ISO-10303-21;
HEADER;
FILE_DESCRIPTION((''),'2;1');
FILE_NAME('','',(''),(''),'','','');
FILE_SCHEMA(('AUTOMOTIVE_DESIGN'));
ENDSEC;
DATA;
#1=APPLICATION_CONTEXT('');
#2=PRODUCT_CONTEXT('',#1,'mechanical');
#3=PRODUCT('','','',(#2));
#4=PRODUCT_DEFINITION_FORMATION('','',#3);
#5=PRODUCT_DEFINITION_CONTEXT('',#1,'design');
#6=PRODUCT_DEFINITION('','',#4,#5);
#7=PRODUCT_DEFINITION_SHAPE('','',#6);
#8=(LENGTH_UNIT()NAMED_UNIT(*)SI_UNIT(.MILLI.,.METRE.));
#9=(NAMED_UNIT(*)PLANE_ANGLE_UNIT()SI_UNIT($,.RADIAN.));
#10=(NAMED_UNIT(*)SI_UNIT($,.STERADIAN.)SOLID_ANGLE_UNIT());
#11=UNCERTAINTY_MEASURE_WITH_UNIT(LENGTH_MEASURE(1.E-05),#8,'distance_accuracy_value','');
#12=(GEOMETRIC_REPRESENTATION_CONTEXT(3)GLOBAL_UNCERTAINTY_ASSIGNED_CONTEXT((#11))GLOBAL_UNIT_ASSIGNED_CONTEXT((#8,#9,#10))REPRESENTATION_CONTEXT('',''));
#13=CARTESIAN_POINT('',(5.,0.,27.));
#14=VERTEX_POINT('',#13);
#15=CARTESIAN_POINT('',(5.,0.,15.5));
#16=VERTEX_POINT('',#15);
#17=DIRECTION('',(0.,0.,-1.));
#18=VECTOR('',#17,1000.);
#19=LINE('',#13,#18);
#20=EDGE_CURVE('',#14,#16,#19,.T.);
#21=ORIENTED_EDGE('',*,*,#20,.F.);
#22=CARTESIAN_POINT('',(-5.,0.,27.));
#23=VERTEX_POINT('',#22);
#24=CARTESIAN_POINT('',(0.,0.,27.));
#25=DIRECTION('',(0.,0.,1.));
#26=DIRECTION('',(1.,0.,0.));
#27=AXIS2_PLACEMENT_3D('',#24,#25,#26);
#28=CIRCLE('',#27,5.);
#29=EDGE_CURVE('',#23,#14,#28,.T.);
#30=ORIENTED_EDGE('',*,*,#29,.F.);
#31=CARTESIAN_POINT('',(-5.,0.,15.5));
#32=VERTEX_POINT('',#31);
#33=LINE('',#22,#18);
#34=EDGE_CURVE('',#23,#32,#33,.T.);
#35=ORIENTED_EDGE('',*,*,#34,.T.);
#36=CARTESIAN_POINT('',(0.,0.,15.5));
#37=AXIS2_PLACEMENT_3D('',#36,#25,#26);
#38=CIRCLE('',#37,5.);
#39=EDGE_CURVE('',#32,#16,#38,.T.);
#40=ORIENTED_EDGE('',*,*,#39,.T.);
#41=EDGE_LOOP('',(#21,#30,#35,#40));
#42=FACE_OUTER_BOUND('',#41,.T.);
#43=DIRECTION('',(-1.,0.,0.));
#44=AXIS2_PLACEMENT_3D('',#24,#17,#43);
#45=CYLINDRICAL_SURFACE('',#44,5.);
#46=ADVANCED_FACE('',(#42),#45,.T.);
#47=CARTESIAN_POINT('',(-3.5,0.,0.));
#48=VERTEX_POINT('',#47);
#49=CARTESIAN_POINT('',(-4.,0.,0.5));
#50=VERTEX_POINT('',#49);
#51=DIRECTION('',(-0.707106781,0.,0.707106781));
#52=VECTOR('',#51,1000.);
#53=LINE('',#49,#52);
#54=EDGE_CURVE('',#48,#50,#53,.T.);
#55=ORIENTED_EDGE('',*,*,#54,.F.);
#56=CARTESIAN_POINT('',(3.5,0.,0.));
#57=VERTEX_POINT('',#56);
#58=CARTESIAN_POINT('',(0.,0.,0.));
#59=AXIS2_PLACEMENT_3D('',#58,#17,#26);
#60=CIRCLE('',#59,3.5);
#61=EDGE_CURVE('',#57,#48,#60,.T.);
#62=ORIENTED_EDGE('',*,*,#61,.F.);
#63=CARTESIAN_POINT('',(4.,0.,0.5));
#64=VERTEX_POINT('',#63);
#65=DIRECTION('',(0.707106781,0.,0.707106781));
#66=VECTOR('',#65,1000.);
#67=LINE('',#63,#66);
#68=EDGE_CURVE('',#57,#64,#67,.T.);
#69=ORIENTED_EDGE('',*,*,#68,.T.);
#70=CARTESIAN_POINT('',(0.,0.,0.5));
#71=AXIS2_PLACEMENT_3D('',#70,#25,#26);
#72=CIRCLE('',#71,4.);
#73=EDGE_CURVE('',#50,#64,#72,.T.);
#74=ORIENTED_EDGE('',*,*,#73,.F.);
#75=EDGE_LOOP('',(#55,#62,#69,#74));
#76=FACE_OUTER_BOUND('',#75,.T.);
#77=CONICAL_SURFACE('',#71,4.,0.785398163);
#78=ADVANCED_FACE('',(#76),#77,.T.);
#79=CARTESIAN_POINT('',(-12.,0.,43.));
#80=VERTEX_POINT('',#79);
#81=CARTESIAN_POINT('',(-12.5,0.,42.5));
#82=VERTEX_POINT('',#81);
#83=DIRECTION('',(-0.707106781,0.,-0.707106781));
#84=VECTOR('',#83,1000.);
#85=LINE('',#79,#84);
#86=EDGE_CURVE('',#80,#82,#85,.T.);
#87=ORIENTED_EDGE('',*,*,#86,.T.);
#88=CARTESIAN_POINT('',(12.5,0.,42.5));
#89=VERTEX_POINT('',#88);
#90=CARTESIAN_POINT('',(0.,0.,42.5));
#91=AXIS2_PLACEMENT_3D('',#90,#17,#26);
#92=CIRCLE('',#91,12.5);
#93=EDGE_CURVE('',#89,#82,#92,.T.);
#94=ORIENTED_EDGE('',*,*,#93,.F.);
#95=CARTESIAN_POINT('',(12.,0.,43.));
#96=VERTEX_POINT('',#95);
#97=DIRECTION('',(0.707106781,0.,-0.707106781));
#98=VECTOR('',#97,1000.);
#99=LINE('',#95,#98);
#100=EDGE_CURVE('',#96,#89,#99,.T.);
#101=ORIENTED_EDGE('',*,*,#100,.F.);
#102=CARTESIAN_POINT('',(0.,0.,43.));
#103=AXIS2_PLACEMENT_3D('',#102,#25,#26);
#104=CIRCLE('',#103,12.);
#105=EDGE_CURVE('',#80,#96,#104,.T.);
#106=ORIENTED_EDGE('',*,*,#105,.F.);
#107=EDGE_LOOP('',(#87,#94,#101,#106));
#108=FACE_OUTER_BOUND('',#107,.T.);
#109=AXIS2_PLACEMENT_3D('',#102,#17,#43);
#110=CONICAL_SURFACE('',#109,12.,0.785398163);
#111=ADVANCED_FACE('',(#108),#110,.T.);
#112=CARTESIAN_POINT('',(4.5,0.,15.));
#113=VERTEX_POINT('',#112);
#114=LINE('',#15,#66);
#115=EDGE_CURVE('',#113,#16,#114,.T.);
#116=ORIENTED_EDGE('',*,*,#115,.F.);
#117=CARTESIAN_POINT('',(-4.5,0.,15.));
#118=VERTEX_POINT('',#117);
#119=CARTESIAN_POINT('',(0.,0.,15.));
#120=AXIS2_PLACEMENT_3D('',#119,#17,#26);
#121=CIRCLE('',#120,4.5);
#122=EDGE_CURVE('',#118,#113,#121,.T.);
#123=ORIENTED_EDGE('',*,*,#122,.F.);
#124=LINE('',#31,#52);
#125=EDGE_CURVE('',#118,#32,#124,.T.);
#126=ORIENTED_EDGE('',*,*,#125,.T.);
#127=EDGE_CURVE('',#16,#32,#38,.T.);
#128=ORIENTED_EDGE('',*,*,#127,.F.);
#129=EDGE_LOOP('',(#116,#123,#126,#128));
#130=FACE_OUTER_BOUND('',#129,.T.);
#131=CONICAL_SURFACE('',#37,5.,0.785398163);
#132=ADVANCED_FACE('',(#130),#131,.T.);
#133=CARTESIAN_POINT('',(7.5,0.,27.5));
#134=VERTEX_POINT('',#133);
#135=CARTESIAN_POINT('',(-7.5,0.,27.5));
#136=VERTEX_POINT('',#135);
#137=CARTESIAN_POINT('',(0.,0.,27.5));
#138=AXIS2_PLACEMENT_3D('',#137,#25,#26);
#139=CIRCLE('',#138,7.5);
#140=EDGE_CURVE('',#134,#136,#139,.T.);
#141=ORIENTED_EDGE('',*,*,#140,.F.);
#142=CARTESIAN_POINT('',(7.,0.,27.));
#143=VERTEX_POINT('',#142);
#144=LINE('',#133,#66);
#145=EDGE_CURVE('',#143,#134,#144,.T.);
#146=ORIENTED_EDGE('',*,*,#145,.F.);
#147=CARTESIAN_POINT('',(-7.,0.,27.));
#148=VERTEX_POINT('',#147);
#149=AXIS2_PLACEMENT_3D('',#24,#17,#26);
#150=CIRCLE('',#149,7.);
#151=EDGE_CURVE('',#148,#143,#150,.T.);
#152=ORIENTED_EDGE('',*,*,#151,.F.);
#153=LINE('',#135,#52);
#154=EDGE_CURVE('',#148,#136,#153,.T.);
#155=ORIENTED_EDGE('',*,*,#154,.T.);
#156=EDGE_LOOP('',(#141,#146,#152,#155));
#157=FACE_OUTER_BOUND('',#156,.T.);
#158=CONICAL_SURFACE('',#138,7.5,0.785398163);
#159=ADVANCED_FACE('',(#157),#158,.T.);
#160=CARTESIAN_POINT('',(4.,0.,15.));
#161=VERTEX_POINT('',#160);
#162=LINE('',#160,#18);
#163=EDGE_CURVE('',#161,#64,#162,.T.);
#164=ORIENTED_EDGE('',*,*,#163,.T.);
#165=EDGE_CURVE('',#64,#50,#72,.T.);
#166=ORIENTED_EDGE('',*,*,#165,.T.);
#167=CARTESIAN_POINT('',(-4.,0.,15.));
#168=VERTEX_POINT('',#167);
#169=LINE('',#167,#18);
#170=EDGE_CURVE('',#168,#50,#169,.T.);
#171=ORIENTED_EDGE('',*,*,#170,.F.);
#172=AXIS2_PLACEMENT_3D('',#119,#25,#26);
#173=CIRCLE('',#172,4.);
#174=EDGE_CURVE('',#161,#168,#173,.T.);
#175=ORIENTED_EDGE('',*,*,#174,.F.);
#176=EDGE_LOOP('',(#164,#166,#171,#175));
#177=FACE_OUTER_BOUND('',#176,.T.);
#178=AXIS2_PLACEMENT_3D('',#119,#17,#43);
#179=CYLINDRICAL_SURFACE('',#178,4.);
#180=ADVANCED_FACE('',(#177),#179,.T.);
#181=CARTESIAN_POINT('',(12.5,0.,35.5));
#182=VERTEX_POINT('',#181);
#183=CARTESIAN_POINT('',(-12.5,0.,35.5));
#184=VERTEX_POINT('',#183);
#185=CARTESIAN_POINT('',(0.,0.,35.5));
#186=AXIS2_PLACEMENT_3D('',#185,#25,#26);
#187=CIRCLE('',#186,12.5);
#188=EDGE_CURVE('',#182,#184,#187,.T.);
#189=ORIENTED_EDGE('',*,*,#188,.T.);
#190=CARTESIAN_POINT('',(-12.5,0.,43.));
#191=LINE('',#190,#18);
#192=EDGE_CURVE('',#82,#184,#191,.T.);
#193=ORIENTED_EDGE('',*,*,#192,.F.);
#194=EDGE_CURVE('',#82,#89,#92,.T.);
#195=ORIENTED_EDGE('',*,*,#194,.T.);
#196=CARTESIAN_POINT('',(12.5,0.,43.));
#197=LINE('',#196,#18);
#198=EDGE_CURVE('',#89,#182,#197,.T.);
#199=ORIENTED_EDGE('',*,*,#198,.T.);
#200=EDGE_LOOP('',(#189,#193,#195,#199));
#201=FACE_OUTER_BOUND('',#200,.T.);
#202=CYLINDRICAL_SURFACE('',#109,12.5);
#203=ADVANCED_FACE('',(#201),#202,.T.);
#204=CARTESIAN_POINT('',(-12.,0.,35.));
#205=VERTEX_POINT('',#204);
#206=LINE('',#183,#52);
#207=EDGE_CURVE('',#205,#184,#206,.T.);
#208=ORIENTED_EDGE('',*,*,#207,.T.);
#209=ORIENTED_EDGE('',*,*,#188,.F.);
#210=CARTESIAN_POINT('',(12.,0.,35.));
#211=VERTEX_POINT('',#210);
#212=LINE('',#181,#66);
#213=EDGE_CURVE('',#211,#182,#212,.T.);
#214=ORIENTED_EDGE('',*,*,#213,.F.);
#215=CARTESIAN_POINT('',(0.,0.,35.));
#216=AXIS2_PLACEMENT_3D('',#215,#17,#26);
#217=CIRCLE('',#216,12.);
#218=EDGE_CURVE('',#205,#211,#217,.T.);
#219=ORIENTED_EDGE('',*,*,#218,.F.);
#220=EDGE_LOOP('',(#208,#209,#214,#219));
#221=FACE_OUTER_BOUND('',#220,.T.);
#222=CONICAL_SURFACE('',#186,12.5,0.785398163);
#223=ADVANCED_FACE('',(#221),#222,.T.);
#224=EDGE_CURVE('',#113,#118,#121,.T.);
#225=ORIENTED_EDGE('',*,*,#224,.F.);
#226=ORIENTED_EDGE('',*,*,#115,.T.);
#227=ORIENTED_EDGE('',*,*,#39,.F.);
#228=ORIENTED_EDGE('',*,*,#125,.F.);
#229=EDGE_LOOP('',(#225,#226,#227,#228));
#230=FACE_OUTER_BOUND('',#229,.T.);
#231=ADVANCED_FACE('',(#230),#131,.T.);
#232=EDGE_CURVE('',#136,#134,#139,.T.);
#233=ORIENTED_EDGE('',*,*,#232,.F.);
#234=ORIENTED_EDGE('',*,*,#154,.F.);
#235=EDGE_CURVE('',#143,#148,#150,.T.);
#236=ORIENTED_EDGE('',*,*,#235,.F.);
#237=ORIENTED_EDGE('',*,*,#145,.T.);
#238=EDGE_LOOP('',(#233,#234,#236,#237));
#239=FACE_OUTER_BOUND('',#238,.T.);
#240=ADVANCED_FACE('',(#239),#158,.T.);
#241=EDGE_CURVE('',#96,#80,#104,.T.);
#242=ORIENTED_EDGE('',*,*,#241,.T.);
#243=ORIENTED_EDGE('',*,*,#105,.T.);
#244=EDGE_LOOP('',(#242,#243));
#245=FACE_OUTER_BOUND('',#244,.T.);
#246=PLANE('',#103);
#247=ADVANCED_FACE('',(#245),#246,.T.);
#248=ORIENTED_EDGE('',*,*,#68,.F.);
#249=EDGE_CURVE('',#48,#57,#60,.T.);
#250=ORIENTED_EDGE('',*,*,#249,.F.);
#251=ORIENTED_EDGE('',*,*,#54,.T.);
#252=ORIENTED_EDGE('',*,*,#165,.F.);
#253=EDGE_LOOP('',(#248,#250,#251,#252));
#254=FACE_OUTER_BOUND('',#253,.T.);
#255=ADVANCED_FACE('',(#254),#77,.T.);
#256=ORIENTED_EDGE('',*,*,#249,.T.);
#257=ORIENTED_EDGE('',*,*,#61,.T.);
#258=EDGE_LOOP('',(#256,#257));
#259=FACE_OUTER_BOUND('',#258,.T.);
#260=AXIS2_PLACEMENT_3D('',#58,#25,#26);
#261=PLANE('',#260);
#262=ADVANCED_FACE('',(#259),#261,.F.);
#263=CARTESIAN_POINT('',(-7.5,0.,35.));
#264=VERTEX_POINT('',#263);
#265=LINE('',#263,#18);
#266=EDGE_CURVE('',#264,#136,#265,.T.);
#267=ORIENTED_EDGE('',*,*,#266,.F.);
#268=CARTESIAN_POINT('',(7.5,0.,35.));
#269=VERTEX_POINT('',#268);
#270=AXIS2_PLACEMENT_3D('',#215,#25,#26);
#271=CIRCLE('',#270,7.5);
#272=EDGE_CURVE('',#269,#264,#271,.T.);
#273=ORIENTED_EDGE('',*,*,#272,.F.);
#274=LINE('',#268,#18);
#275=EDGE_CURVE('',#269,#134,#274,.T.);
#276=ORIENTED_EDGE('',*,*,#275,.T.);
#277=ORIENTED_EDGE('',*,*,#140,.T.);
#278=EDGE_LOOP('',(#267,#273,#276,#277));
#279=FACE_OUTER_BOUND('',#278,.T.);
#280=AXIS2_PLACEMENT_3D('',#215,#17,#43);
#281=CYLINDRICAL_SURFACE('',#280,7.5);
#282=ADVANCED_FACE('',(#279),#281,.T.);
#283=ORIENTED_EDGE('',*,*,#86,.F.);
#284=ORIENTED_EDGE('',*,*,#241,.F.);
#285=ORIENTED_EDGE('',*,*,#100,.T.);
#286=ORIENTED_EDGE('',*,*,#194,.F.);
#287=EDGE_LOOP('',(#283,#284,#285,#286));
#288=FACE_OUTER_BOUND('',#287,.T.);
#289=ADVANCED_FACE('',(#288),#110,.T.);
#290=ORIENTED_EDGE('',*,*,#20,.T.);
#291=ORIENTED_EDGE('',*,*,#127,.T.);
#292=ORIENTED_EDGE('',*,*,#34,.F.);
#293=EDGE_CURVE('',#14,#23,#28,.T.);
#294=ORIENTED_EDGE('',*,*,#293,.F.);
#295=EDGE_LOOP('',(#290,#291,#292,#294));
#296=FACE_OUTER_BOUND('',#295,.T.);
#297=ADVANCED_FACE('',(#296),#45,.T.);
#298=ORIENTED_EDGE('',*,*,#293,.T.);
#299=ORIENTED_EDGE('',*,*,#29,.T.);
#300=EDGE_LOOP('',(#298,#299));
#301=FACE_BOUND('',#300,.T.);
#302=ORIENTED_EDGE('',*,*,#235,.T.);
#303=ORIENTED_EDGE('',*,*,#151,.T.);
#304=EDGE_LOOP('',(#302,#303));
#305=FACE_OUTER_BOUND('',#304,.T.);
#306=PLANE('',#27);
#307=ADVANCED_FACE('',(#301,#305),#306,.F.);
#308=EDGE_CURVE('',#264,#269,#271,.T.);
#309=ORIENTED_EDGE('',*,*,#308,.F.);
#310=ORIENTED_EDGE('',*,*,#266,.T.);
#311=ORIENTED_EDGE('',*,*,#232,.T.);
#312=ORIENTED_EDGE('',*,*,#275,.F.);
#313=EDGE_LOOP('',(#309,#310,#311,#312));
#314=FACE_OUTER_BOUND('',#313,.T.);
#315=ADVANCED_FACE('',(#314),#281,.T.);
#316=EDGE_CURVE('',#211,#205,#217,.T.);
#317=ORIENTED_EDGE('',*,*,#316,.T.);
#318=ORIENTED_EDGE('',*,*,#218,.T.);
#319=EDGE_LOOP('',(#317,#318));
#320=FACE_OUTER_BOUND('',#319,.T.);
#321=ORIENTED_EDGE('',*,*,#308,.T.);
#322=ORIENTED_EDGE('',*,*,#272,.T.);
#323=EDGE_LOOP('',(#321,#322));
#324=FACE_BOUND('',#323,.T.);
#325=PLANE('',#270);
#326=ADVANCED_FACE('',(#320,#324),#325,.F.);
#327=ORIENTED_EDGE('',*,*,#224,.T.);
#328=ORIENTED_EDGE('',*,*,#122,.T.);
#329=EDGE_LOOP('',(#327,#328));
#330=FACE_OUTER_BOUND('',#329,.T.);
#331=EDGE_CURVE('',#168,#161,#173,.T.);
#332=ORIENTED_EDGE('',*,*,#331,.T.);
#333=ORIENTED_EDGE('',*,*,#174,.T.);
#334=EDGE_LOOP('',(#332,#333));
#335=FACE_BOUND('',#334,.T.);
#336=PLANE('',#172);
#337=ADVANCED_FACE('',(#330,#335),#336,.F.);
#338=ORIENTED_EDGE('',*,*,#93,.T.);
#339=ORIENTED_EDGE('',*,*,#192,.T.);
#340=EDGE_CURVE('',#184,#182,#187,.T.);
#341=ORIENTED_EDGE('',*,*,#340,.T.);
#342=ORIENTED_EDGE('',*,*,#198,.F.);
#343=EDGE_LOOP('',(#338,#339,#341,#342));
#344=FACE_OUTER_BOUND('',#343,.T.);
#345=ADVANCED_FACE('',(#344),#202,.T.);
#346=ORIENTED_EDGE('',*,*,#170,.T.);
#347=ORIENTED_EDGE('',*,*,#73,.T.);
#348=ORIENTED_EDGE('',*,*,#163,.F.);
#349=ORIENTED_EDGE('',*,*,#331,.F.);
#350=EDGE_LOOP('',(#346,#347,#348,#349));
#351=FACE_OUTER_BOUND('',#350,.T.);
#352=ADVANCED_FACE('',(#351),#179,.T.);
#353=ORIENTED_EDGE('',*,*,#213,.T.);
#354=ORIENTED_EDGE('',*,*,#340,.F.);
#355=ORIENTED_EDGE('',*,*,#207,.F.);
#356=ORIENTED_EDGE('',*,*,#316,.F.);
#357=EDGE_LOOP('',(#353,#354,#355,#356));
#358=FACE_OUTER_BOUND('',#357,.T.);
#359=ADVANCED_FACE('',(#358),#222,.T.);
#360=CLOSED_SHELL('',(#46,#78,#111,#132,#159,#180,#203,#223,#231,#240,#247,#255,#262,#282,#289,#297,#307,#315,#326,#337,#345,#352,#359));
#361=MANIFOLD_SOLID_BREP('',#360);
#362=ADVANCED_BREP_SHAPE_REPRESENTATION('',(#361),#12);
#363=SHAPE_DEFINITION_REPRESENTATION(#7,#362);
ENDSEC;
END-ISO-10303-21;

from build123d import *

# Parameters (mm, degrees)
SKETCH1_R           = 4
BOSS_EXTRUDE1_DEPTH = 15
SKETCH2_R           = 5
BOSS_EXTRUDE2_DEPTH = 12
SKETCH3_R           = 7.5
BOSS_EXTRUDE3_DEPTH = 8
SKETCH4_R           = 12.5
BOSS_EXTRUDE4_DEPTH = 8
CHAMFER1_SIZE       = 0.5


with BuildPart() as part:
    # Sketch1 → Boss-Extrude1 (new body)
    with BuildSketch(Plane.XY):
        Circle(SKETCH1_R)
    extrude(amount=BOSS_EXTRUDE1_DEPTH)

    # Sketch2 → Boss-Extrude2 (add)
    with BuildSketch(Plane.XY.offset(15)):
        Circle(SKETCH2_R)
    extrude(amount=BOSS_EXTRUDE2_DEPTH)

    # Sketch3 → Boss-Extrude3 (add)
    with BuildSketch(Plane.XY.offset(27)):
        Circle(SKETCH3_R)
    extrude(amount=BOSS_EXTRUDE3_DEPTH)

    # Sketch4 → Boss-Extrude4 (add)
    with BuildSketch(Plane.XY.offset(35)):
        Circle(SKETCH4_R)
    extrude(amount=BOSS_EXTRUDE4_DEPTH)

    # Chamfer1
    chamfer1_edges = [part.edges().sort_by_distance(p)[0] for p in [
        (-12.5, 0, 35),
        (-12.5, 0, 43),
        (-4, 0, 0),
        (-5, 0, 15),
        (-7.5, 0, 27),
    ]]
    chamfer(chamfer1_edges, length=CHAMFER1_SIZE)


solid = part.part
